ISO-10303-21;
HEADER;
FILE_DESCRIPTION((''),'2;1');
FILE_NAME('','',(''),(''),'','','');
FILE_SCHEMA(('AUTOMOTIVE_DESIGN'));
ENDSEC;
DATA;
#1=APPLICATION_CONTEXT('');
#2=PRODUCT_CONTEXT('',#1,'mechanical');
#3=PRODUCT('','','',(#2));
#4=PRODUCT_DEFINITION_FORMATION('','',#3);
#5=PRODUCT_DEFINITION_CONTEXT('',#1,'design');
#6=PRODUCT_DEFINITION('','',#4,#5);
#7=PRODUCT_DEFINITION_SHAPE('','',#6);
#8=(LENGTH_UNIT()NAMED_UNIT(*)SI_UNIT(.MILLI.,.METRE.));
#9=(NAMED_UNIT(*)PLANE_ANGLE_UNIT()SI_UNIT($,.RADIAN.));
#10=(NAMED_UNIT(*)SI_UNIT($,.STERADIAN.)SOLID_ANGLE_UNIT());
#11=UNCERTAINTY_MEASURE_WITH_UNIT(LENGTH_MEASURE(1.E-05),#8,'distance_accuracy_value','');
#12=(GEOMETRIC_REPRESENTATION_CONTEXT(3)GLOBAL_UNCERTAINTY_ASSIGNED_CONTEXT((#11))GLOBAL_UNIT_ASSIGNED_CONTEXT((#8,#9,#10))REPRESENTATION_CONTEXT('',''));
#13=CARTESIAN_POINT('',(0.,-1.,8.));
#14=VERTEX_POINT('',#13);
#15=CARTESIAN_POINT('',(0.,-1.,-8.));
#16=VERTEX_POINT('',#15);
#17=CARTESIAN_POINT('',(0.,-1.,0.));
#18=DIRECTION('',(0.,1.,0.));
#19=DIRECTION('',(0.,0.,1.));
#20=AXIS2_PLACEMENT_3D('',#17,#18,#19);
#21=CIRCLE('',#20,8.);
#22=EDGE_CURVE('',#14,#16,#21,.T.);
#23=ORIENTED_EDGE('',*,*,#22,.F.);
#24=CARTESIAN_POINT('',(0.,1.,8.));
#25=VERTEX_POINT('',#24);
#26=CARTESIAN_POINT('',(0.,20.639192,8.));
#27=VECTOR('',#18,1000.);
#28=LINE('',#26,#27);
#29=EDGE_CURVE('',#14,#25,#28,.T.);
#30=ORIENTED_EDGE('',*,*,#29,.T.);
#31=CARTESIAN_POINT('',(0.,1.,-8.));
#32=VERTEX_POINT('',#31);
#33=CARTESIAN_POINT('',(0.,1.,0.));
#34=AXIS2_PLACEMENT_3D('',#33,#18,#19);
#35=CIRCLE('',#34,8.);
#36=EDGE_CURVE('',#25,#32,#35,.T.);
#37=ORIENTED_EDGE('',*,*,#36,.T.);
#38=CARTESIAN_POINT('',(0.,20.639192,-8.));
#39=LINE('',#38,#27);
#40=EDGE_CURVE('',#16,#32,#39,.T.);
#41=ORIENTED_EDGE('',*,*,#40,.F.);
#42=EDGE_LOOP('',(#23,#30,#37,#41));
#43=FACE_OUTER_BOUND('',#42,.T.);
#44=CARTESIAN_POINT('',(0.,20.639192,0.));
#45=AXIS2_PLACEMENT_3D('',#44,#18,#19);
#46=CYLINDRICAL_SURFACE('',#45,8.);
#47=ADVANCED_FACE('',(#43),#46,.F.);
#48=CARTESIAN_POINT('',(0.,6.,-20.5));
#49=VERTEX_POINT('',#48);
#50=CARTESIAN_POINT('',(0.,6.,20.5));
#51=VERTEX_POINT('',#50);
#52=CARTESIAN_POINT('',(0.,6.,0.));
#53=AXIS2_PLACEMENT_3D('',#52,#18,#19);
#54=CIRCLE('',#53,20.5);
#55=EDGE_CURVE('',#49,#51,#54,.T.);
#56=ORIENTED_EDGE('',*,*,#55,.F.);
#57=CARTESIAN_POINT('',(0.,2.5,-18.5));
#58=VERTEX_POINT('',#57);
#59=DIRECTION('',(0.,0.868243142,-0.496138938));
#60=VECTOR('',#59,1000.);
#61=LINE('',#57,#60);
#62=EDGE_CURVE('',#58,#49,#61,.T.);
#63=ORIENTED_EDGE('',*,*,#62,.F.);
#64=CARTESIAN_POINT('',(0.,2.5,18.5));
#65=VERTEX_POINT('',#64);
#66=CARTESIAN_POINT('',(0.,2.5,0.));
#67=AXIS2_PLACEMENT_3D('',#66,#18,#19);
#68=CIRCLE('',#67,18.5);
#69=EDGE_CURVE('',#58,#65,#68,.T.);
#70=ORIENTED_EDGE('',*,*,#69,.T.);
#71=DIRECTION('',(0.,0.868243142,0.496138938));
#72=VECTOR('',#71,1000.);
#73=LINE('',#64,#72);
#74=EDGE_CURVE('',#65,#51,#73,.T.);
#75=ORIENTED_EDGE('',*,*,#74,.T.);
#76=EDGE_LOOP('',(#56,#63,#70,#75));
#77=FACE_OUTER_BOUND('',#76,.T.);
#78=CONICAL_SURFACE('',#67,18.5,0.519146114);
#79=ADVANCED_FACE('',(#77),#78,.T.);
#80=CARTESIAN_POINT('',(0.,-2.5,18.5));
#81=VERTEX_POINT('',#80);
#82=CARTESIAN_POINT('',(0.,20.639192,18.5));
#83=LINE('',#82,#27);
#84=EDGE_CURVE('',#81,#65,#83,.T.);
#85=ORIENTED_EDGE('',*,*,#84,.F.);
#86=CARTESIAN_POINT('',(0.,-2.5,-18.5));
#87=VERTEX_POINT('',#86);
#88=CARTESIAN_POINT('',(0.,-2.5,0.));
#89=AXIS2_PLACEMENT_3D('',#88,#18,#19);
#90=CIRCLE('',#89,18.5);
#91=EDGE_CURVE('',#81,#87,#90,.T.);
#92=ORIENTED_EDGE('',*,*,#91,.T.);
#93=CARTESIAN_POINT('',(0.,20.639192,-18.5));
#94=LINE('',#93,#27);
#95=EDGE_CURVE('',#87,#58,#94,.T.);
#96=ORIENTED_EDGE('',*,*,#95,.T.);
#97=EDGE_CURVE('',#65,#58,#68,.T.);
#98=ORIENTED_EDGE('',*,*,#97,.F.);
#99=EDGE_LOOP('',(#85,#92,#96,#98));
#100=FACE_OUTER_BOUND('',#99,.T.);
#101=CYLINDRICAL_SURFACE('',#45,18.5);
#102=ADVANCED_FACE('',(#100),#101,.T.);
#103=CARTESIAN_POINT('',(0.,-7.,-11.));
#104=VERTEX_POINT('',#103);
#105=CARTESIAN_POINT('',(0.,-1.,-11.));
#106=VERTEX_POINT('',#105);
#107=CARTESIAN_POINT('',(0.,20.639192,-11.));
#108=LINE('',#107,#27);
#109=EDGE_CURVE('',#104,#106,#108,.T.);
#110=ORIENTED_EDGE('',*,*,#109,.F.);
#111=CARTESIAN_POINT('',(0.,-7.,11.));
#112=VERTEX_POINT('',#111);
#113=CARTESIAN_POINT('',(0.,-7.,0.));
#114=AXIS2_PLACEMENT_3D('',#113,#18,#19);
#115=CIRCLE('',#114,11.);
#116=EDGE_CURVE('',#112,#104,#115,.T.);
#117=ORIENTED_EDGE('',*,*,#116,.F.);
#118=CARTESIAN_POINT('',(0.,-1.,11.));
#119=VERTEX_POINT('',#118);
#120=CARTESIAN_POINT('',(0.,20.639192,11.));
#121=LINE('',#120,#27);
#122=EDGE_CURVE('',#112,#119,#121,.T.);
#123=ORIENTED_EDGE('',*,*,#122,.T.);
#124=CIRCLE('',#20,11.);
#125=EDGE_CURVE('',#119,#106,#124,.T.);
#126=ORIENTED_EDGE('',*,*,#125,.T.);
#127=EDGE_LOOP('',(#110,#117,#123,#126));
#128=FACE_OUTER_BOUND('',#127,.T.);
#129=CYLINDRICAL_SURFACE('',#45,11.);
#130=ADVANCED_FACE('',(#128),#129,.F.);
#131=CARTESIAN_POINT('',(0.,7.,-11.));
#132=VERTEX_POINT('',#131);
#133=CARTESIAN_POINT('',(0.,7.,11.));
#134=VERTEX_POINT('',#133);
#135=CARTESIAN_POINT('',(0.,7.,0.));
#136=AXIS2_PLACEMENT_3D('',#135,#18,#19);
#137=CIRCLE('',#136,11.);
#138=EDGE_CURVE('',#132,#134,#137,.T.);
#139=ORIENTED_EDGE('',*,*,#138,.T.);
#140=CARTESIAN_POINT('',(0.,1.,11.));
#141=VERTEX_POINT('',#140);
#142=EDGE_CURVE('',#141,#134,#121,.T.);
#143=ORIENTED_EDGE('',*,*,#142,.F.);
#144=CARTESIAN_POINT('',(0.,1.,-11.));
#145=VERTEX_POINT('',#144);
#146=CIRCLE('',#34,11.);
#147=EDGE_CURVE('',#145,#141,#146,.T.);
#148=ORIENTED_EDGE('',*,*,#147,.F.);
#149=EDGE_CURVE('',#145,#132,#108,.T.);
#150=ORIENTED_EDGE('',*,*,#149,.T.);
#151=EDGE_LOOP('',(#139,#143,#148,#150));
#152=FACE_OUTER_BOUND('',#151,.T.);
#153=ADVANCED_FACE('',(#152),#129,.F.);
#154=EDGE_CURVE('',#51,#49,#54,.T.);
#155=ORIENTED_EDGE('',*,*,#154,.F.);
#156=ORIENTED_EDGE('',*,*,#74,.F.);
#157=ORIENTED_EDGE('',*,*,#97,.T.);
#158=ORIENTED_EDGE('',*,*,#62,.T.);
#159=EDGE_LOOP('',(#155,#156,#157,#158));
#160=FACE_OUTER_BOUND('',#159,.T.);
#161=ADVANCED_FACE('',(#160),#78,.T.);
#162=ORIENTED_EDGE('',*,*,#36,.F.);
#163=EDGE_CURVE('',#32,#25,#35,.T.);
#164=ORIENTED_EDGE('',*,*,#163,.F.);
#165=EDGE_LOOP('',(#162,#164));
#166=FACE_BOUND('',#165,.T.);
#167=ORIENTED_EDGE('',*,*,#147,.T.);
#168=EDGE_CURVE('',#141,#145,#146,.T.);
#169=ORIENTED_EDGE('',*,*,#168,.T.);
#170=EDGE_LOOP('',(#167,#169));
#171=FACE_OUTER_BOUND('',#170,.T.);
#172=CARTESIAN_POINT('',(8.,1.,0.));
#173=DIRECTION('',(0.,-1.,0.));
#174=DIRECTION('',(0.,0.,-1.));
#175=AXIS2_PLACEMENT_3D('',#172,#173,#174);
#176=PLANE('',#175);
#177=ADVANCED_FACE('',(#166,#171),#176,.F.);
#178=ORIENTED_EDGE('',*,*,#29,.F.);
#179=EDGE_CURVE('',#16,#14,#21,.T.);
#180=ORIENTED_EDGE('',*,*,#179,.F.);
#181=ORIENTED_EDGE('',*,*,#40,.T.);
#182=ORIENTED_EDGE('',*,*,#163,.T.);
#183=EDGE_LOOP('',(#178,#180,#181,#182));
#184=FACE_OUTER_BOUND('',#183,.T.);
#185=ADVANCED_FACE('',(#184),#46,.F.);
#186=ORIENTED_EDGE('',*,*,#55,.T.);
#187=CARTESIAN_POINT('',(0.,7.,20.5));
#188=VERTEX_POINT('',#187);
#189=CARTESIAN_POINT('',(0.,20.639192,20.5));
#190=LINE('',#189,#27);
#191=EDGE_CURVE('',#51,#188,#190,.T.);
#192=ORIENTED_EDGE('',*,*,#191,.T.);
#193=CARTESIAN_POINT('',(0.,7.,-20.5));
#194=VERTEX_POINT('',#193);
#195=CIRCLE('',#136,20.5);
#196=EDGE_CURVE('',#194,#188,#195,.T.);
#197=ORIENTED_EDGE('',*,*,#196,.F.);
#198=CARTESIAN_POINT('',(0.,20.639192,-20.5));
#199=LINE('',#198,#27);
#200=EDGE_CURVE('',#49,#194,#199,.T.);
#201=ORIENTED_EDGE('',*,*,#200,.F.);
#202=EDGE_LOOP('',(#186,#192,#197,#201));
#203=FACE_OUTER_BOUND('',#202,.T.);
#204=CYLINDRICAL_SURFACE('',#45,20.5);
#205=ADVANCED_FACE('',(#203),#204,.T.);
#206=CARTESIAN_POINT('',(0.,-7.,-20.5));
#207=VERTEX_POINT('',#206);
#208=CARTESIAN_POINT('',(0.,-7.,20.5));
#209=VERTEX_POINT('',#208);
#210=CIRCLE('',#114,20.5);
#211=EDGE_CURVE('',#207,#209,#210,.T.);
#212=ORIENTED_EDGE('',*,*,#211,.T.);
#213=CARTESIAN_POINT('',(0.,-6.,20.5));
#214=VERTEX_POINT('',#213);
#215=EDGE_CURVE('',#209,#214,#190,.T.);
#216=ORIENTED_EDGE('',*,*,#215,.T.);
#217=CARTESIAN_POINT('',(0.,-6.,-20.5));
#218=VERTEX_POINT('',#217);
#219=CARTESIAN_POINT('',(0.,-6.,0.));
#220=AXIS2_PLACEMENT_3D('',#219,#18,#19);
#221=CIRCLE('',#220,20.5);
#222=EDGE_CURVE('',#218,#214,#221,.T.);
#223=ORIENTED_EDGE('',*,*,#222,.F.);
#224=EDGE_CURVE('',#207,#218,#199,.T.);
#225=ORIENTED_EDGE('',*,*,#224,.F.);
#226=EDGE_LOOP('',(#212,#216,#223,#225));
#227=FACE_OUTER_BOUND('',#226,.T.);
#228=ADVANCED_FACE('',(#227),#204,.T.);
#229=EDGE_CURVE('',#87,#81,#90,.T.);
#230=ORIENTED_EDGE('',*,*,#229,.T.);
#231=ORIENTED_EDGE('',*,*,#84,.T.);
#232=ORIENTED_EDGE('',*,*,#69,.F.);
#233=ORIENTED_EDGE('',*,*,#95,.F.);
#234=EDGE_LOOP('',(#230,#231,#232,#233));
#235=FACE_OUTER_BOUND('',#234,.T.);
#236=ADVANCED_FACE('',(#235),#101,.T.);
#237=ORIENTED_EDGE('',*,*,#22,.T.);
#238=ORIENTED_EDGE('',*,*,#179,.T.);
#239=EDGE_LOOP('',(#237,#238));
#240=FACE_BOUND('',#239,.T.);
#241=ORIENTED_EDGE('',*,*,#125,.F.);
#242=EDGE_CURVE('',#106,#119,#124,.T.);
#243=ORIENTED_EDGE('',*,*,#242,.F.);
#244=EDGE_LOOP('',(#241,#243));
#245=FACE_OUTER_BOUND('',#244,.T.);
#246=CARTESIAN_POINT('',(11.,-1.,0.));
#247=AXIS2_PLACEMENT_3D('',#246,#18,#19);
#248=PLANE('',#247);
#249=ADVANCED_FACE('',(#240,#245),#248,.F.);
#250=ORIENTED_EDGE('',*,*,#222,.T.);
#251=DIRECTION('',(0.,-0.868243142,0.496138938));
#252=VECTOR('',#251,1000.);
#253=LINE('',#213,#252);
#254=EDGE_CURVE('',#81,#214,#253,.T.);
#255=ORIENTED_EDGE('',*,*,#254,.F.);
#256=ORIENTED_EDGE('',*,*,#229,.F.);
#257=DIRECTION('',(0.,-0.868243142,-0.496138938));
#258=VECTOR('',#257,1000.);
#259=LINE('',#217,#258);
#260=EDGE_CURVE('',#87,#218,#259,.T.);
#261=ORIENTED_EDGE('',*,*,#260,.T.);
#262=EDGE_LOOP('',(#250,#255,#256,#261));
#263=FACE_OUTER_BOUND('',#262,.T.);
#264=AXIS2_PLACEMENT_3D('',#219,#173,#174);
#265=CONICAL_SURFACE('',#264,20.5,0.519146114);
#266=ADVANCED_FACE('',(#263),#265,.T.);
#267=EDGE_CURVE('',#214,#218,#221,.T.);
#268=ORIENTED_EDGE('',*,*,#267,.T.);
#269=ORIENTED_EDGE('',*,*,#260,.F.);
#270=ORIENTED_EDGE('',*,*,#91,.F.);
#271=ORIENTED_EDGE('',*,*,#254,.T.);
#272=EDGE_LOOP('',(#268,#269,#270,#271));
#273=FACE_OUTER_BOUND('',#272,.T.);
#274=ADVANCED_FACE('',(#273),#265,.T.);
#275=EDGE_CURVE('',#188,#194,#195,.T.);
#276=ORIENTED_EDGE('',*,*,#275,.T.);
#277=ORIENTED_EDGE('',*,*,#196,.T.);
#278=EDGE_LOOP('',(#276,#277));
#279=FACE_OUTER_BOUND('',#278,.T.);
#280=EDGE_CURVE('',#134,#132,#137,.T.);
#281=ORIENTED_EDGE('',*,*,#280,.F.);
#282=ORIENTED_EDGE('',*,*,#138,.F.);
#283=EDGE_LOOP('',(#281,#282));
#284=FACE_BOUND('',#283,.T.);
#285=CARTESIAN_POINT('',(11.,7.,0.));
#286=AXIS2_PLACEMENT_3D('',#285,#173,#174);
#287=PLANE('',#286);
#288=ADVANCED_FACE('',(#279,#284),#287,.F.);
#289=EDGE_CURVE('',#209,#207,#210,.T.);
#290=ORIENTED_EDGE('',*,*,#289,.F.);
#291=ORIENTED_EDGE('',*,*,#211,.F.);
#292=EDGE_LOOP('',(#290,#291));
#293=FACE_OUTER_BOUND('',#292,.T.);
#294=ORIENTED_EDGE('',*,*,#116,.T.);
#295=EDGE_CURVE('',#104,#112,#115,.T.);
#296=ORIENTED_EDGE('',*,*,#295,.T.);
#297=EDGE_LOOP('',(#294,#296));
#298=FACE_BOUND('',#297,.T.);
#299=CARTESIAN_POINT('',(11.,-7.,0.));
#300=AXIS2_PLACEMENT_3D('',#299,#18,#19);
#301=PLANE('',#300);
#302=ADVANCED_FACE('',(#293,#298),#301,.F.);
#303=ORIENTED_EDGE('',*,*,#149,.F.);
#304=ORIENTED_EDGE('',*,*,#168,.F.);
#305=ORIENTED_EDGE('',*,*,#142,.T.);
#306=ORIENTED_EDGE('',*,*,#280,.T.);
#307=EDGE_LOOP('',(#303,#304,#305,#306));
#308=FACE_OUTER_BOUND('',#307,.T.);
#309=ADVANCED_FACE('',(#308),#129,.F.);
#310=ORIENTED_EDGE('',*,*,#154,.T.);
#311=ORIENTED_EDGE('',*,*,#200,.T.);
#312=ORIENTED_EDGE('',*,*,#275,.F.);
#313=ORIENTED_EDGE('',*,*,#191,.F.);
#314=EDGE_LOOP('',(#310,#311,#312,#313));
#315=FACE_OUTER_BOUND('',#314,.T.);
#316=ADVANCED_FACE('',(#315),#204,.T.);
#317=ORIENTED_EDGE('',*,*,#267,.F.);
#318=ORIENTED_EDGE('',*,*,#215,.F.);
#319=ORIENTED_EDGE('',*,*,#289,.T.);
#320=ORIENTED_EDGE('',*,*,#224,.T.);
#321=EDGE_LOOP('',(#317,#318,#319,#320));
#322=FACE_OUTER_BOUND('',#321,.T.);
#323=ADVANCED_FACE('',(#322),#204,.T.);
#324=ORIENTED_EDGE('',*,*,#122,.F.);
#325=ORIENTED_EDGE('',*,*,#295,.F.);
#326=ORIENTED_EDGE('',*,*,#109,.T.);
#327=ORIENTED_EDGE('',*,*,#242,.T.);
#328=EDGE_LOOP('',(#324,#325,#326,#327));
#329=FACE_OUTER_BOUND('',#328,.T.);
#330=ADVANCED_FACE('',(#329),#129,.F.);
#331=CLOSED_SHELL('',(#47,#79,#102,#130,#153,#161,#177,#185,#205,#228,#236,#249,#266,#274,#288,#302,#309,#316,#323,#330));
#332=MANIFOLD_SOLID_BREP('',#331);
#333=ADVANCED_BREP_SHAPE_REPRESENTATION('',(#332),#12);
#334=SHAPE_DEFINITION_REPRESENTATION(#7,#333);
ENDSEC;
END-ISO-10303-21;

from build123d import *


with BuildPart() as part:
    # 草图1 → 旋转1 (revolve)
    with BuildSketch(Plane.XY, mode=Mode.PRIVATE) as revolve_1_sk:
        Polygon((20.5, -6), (18.5, -2.5), (18.5, 2.5), (20.5, 6), (20.5, 7), (11, 7), (11, 1), (8, 1), (8, -1), (11, -1), (11, -7), (20.5, -7), align=None)
    revolve(revolve_1_sk.sketch.rotate(Axis((0, 20.639192491, 0), (0, -1, 0)), 90), axis=Axis((0, 20.639192491, 0), (0, -1, 0)))


solid = part.part
